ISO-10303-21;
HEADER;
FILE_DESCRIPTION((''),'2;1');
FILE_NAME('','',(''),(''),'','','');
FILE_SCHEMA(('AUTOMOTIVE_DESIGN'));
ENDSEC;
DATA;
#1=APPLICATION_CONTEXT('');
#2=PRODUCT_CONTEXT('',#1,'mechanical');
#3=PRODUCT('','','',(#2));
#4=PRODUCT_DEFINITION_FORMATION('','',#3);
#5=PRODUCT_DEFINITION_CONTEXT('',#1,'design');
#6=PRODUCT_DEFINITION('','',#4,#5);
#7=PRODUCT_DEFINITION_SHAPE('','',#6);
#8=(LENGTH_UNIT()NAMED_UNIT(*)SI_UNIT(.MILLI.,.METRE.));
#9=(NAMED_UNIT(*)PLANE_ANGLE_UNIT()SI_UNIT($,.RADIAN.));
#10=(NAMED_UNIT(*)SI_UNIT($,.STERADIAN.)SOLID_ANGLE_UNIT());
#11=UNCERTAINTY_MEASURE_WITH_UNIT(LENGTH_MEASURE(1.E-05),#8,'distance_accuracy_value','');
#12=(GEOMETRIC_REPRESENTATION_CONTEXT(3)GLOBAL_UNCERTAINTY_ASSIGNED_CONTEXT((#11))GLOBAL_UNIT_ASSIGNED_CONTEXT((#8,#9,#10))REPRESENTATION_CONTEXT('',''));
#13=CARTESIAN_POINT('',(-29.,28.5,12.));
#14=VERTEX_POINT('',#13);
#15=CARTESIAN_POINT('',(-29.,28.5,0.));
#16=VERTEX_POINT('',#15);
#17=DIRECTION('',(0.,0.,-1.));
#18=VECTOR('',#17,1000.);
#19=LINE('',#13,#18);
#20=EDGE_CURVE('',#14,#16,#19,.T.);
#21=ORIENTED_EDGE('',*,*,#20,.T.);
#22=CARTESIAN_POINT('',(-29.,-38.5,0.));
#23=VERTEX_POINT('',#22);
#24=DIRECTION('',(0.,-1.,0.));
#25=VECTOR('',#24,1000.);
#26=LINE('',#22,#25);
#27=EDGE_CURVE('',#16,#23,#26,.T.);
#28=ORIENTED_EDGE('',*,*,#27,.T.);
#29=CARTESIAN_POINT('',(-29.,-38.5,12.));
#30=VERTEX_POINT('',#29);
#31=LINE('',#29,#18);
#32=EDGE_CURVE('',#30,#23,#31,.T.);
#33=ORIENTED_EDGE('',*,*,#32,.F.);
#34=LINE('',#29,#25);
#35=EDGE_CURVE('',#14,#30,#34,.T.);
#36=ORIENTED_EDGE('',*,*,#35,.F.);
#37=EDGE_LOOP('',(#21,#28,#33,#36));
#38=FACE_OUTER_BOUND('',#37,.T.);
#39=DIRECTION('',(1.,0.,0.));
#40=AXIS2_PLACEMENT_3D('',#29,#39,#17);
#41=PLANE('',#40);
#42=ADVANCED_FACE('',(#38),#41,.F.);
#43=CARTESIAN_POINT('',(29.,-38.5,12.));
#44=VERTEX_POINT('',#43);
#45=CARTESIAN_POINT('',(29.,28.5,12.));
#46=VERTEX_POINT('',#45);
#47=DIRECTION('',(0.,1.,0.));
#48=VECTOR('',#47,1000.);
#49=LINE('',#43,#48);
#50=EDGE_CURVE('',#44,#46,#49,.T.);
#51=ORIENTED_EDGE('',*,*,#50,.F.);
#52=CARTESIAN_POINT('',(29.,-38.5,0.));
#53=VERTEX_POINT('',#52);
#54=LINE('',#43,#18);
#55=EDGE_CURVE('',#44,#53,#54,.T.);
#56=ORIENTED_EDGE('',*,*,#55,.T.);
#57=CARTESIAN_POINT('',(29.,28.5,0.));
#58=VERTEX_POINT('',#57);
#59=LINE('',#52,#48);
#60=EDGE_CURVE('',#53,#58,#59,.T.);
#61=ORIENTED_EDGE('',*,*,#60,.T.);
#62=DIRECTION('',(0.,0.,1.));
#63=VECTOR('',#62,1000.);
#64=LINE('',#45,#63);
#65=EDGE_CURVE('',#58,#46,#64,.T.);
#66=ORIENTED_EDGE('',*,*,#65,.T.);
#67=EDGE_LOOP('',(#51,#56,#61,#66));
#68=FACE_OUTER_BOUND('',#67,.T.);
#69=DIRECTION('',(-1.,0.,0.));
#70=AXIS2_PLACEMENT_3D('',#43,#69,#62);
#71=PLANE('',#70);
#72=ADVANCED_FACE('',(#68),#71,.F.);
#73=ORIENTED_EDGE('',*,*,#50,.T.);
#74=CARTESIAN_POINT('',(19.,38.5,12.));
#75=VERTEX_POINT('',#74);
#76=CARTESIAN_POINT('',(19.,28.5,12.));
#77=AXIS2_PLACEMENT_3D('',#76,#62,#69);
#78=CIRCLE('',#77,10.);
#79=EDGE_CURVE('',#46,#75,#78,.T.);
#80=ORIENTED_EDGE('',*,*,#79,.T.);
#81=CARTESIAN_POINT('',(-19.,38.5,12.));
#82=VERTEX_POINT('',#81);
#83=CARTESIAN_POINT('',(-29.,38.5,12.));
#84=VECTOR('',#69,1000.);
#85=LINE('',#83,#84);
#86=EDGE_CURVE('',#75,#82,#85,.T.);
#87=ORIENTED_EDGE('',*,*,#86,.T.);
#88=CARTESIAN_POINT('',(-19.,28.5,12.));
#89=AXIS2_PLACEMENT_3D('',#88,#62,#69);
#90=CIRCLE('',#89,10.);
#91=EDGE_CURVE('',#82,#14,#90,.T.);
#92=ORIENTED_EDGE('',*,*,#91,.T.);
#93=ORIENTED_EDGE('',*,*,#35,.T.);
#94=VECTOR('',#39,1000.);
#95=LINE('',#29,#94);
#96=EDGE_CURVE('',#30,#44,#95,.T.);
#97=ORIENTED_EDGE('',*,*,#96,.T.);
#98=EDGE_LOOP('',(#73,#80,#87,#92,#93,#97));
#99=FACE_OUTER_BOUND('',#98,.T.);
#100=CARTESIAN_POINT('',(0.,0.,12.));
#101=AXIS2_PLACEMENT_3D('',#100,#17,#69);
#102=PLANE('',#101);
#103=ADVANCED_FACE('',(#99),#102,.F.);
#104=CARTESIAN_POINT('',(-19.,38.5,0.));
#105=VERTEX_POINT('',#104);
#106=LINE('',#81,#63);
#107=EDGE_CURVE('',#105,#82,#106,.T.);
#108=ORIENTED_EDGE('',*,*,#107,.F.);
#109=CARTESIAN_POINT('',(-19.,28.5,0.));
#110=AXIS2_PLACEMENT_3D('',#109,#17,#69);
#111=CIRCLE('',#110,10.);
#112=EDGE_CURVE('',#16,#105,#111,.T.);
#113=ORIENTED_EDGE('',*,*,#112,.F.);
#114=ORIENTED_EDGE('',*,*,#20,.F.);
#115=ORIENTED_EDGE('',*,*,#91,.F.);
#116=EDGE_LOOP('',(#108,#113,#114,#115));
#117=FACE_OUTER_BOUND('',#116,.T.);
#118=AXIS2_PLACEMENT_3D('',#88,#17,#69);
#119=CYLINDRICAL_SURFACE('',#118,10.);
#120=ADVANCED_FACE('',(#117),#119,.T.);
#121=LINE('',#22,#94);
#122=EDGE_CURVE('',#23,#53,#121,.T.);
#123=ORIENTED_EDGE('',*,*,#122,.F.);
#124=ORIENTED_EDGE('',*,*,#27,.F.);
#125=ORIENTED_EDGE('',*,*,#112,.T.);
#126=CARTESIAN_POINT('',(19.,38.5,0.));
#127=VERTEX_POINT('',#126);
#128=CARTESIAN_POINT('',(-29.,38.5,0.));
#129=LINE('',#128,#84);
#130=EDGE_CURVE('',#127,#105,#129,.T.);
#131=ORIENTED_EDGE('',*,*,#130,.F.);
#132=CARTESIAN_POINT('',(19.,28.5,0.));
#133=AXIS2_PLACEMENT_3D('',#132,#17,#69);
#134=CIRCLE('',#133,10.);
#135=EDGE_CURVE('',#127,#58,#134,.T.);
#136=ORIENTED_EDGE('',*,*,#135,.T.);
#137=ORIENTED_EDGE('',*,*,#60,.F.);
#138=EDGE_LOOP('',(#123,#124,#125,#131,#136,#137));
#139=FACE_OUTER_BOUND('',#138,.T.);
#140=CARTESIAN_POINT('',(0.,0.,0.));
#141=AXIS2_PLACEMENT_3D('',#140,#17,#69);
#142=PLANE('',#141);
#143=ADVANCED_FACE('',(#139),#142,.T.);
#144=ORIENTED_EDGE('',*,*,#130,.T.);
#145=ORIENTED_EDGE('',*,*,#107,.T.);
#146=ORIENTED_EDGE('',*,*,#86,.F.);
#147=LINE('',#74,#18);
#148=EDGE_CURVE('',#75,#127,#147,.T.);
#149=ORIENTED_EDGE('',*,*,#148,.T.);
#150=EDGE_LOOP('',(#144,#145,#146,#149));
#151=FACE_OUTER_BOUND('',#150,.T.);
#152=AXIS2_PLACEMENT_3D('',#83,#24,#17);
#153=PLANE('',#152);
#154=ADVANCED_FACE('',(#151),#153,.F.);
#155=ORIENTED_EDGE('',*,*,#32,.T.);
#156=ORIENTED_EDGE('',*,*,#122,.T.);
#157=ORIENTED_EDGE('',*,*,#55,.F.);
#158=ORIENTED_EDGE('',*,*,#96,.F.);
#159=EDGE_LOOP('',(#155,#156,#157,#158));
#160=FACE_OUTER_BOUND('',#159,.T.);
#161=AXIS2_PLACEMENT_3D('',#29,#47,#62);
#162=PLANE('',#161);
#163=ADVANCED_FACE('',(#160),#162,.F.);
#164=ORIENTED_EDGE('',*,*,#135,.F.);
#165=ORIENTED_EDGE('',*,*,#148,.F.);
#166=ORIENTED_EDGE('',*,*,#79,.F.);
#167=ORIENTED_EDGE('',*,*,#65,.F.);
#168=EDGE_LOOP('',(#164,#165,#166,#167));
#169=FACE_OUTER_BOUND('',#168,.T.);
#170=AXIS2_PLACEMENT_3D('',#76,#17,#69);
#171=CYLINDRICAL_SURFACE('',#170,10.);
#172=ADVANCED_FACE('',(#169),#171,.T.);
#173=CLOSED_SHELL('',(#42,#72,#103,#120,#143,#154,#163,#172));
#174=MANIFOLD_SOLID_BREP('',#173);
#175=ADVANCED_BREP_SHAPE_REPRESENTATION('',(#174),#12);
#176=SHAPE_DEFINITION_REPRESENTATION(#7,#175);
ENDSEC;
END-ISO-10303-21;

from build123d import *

# Parameters (mm, degrees)
SKETCH1_W           = 58
SKETCH1_H           = 77
BOSS_EXTRUDE1_DEPTH = 12
FILLET1_R           = 10


with BuildPart() as part:
    # Sketch1 → Boss-Extrude1 (new body)
    with BuildSketch(Plane.XY):
        Rectangle(SKETCH1_W, SKETCH1_H)
    extrude(amount=BOSS_EXTRUDE1_DEPTH)

    # Fillet1
    fillet1_edges = [part.edges().sort_by_distance(p)[0] for p in [
        (-29, 38.5, 6),
        (29, 38.5, 6),
    ]]
    fillet(fillet1_edges, radius=FILLET1_R)


solid = part.part
